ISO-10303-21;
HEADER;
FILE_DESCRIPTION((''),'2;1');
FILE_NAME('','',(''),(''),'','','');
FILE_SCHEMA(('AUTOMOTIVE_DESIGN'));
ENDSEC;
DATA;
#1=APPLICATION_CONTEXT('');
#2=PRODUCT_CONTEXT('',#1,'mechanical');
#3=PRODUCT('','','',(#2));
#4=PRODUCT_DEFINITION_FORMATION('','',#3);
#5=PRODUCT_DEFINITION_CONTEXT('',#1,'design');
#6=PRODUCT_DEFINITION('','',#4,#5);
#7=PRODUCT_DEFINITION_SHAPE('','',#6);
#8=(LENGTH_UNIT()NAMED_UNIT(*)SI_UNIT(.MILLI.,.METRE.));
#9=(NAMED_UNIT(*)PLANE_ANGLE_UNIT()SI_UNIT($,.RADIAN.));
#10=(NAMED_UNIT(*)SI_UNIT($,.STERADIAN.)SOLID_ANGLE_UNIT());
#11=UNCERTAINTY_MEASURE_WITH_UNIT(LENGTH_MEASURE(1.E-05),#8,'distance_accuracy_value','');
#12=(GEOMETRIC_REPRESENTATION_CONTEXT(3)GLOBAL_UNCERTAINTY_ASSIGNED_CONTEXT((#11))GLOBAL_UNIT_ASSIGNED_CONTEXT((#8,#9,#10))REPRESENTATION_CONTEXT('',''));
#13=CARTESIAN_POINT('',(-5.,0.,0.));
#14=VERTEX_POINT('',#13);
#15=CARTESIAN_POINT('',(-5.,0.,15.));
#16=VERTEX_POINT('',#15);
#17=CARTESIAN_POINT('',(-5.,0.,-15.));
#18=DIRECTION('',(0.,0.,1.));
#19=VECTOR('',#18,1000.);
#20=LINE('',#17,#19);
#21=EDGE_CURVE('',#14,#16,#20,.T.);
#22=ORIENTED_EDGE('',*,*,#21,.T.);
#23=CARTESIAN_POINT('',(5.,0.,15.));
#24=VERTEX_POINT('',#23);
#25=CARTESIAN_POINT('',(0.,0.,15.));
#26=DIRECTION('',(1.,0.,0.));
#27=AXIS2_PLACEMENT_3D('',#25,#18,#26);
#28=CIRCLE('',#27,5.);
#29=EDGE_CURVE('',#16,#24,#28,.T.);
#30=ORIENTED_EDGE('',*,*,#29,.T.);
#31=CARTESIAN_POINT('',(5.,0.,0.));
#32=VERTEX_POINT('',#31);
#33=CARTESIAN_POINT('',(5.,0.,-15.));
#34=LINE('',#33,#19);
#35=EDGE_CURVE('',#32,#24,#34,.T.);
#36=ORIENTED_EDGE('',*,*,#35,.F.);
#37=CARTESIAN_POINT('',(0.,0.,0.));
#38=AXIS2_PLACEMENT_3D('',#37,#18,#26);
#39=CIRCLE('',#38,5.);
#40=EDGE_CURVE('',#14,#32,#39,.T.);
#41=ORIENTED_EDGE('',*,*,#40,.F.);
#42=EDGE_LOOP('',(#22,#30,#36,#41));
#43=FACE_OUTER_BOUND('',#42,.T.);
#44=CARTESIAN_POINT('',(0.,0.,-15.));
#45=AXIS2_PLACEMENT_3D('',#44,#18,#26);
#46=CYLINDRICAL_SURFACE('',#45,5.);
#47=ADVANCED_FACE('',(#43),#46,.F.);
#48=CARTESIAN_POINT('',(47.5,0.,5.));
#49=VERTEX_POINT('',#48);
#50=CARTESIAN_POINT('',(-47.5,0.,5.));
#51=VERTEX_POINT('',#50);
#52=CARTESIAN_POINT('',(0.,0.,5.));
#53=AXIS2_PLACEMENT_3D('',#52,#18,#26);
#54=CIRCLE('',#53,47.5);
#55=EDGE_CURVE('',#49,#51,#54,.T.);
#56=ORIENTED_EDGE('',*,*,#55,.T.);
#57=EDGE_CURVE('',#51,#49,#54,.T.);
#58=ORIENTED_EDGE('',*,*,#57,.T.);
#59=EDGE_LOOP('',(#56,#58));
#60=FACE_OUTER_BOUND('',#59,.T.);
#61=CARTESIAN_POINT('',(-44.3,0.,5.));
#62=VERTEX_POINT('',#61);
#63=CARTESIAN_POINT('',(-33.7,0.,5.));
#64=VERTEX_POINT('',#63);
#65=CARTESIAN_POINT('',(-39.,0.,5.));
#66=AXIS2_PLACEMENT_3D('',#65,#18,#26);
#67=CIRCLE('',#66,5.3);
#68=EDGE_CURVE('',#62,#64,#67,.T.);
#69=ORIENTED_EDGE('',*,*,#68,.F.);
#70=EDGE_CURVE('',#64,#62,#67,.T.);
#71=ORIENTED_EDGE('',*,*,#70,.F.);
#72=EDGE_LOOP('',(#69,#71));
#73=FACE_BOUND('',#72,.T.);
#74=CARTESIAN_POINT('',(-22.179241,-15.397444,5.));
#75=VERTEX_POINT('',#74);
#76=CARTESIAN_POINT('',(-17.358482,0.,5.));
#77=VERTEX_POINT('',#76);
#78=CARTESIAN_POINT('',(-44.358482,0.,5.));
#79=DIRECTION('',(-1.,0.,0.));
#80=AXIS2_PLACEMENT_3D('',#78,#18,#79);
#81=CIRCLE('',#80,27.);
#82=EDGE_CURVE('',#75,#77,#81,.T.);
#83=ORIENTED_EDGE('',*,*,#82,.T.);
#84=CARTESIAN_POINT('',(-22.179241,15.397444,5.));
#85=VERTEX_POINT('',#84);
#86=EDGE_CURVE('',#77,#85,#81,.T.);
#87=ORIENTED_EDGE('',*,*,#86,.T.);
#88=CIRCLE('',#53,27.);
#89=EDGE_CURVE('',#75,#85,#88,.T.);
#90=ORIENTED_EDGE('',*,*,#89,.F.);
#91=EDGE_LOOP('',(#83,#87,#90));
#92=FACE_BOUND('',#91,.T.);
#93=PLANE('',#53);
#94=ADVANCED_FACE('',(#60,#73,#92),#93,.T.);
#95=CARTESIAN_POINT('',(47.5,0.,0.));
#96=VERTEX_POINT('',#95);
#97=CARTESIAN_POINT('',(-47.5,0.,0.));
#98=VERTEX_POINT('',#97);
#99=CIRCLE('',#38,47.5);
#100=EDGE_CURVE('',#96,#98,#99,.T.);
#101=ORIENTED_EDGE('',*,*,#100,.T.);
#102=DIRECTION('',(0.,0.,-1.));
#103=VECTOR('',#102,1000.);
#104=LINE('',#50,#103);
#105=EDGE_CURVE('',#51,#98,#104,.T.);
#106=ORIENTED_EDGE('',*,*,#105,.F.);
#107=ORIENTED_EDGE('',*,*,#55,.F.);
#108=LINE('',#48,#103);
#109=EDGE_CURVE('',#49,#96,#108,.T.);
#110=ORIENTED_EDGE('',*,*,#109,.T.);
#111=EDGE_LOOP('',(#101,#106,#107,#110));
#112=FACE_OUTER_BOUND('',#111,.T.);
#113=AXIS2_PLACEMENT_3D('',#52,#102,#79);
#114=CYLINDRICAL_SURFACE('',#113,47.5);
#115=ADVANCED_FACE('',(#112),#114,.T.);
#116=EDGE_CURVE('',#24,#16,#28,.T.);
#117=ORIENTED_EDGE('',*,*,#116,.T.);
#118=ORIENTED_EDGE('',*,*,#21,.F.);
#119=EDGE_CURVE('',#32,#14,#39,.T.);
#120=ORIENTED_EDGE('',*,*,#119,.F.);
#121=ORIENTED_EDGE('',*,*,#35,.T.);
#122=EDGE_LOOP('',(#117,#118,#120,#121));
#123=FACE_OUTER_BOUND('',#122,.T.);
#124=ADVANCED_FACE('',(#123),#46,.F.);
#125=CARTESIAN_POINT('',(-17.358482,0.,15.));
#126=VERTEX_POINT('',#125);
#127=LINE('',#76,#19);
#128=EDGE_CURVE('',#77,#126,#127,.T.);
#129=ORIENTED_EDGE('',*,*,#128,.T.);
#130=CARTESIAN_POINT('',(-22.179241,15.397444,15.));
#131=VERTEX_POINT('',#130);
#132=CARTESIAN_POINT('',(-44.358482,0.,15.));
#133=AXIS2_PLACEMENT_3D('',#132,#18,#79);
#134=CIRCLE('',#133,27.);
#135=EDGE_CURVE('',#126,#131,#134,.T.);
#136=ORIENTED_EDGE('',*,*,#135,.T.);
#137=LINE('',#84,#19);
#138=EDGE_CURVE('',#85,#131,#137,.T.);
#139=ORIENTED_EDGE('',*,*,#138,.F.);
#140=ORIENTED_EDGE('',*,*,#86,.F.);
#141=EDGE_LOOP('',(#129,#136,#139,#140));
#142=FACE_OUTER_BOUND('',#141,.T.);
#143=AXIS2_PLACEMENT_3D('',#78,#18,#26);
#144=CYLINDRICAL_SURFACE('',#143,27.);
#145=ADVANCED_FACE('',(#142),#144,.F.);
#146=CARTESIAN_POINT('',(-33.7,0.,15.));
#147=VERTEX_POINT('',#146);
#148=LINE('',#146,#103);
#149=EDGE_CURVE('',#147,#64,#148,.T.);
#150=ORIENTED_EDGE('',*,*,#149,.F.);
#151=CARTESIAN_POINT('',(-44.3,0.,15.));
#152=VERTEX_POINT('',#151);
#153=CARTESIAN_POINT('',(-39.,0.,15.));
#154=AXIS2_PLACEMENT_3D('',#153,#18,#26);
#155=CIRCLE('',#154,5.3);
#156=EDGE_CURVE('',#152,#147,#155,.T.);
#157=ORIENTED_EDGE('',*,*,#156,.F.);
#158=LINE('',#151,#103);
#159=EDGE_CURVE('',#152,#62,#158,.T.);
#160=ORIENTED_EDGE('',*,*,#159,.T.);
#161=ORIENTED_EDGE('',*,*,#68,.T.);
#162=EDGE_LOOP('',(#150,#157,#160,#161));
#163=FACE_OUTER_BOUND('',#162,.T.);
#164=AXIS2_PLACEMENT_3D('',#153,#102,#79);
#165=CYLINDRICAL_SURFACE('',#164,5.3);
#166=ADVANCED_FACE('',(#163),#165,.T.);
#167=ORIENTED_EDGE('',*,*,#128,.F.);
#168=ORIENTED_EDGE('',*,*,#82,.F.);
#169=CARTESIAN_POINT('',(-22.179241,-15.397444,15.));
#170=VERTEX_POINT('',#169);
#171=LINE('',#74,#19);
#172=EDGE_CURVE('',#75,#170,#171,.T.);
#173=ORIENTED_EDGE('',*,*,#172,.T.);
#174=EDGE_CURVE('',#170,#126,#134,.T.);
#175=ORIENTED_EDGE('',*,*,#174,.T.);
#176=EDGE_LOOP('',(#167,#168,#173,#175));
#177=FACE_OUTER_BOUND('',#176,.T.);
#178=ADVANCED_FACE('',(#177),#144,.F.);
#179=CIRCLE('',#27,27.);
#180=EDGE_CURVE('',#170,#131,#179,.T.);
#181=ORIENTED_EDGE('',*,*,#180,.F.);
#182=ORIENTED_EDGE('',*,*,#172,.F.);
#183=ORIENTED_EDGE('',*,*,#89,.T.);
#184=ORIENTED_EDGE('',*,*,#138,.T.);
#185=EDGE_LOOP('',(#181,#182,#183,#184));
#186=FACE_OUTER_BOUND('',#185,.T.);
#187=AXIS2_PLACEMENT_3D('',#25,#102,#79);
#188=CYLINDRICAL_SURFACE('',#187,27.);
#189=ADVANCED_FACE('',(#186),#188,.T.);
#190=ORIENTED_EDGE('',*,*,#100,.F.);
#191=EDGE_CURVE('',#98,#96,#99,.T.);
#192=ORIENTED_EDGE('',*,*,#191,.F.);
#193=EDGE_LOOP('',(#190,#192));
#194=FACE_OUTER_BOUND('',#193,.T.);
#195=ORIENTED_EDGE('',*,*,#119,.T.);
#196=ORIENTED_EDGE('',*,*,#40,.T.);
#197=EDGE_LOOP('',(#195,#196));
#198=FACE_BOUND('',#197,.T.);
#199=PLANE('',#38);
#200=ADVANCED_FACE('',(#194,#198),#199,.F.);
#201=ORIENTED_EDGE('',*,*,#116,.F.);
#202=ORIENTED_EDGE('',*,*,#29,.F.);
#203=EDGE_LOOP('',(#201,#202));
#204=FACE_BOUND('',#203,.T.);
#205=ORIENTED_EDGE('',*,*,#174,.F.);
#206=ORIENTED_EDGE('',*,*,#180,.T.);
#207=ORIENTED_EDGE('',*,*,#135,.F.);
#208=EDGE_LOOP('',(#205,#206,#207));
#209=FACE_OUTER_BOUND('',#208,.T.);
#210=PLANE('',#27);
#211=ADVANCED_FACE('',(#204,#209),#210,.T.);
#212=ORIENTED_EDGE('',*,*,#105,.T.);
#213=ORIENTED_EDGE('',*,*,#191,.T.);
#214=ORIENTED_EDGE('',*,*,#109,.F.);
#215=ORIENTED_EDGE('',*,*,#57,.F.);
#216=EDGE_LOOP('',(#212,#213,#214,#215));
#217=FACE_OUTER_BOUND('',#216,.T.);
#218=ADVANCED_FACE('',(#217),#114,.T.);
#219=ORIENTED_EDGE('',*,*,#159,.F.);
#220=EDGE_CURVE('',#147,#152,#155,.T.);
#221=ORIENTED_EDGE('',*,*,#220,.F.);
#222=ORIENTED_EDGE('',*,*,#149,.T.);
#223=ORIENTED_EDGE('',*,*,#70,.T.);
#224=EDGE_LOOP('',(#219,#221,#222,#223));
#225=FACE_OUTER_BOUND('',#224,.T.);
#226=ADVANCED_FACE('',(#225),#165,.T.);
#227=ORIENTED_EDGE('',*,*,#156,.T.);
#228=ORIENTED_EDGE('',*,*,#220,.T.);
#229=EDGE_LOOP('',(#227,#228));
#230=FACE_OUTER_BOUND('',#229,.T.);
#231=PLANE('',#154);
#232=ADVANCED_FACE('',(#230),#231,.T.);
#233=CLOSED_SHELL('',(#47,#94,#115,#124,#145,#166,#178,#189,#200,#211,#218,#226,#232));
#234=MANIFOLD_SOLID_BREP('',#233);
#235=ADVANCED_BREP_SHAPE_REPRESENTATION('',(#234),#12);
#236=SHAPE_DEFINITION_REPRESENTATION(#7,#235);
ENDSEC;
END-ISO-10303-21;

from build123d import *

# Parameters (mm, degrees)
DISC_PROFILE_R        = 47.5
DISC_95X5_DEPTH       = 5
DRIVE_PIN_PROFILE_R   = 5.3
DRIVE_PIN_10_6_DEPTH  = 10
HUB_PROFILE_R         = 27
HUB_54X10_DEPTH       = 10
HUB_START             = -10
HUB_FLAT_CUT_DEPTH    = 10
CENTRE_BORE_PROFILE_R = 5
CENTRE_BORE_10_DEPTH  = 30


with BuildPart() as part:
    # Disc Profile → Disc Ø95x5 (new body)
    with BuildSketch(Plane.XY):
        Circle(DISC_PROFILE_R)
    extrude(amount=DISC_95X5_DEPTH)

    # Drive Pin Profile → Drive Pin Ø10.6 (add)
    with BuildSketch(Plane.XY.offset(5)):
        with Locations((-39, 0)):
            Circle(DRIVE_PIN_PROFILE_R)
    extrude(amount=DRIVE_PIN_10_6_DEPTH)

    # Hub Profile → Hub Ø54x10 (add)
    with BuildSketch(Plane.XY.offset(5)):
        Circle(HUB_PROFILE_R)
    extrude(amount=HUB_54X10_DEPTH)

    # Hub Flat Profile → Hub Flat Cut (cut)
    with BuildSketch(Plane.XY.offset(15).offset(HUB_START)):
        with BuildLine():
            ThreePointArc((-22.179240987, 15.397443595), (-27, 0), (-22.179240987, -15.397443595))
            ThreePointArc((-22.179240987, -15.397443595), (-17.358481974, 0), (-22.179240987, 15.397443595))
        make_face()
    extrude(amount=HUB_FLAT_CUT_DEPTH, mode=Mode.SUBTRACT)

    # Centre Bore Profile → Centre Bore Ø10 (cut)
    with BuildSketch(Plane.XY.offset(15)):
        Circle(CENTRE_BORE_PROFILE_R)
    extrude(amount=-CENTRE_BORE_10_DEPTH, mode=Mode.SUBTRACT)


solid = part.part
